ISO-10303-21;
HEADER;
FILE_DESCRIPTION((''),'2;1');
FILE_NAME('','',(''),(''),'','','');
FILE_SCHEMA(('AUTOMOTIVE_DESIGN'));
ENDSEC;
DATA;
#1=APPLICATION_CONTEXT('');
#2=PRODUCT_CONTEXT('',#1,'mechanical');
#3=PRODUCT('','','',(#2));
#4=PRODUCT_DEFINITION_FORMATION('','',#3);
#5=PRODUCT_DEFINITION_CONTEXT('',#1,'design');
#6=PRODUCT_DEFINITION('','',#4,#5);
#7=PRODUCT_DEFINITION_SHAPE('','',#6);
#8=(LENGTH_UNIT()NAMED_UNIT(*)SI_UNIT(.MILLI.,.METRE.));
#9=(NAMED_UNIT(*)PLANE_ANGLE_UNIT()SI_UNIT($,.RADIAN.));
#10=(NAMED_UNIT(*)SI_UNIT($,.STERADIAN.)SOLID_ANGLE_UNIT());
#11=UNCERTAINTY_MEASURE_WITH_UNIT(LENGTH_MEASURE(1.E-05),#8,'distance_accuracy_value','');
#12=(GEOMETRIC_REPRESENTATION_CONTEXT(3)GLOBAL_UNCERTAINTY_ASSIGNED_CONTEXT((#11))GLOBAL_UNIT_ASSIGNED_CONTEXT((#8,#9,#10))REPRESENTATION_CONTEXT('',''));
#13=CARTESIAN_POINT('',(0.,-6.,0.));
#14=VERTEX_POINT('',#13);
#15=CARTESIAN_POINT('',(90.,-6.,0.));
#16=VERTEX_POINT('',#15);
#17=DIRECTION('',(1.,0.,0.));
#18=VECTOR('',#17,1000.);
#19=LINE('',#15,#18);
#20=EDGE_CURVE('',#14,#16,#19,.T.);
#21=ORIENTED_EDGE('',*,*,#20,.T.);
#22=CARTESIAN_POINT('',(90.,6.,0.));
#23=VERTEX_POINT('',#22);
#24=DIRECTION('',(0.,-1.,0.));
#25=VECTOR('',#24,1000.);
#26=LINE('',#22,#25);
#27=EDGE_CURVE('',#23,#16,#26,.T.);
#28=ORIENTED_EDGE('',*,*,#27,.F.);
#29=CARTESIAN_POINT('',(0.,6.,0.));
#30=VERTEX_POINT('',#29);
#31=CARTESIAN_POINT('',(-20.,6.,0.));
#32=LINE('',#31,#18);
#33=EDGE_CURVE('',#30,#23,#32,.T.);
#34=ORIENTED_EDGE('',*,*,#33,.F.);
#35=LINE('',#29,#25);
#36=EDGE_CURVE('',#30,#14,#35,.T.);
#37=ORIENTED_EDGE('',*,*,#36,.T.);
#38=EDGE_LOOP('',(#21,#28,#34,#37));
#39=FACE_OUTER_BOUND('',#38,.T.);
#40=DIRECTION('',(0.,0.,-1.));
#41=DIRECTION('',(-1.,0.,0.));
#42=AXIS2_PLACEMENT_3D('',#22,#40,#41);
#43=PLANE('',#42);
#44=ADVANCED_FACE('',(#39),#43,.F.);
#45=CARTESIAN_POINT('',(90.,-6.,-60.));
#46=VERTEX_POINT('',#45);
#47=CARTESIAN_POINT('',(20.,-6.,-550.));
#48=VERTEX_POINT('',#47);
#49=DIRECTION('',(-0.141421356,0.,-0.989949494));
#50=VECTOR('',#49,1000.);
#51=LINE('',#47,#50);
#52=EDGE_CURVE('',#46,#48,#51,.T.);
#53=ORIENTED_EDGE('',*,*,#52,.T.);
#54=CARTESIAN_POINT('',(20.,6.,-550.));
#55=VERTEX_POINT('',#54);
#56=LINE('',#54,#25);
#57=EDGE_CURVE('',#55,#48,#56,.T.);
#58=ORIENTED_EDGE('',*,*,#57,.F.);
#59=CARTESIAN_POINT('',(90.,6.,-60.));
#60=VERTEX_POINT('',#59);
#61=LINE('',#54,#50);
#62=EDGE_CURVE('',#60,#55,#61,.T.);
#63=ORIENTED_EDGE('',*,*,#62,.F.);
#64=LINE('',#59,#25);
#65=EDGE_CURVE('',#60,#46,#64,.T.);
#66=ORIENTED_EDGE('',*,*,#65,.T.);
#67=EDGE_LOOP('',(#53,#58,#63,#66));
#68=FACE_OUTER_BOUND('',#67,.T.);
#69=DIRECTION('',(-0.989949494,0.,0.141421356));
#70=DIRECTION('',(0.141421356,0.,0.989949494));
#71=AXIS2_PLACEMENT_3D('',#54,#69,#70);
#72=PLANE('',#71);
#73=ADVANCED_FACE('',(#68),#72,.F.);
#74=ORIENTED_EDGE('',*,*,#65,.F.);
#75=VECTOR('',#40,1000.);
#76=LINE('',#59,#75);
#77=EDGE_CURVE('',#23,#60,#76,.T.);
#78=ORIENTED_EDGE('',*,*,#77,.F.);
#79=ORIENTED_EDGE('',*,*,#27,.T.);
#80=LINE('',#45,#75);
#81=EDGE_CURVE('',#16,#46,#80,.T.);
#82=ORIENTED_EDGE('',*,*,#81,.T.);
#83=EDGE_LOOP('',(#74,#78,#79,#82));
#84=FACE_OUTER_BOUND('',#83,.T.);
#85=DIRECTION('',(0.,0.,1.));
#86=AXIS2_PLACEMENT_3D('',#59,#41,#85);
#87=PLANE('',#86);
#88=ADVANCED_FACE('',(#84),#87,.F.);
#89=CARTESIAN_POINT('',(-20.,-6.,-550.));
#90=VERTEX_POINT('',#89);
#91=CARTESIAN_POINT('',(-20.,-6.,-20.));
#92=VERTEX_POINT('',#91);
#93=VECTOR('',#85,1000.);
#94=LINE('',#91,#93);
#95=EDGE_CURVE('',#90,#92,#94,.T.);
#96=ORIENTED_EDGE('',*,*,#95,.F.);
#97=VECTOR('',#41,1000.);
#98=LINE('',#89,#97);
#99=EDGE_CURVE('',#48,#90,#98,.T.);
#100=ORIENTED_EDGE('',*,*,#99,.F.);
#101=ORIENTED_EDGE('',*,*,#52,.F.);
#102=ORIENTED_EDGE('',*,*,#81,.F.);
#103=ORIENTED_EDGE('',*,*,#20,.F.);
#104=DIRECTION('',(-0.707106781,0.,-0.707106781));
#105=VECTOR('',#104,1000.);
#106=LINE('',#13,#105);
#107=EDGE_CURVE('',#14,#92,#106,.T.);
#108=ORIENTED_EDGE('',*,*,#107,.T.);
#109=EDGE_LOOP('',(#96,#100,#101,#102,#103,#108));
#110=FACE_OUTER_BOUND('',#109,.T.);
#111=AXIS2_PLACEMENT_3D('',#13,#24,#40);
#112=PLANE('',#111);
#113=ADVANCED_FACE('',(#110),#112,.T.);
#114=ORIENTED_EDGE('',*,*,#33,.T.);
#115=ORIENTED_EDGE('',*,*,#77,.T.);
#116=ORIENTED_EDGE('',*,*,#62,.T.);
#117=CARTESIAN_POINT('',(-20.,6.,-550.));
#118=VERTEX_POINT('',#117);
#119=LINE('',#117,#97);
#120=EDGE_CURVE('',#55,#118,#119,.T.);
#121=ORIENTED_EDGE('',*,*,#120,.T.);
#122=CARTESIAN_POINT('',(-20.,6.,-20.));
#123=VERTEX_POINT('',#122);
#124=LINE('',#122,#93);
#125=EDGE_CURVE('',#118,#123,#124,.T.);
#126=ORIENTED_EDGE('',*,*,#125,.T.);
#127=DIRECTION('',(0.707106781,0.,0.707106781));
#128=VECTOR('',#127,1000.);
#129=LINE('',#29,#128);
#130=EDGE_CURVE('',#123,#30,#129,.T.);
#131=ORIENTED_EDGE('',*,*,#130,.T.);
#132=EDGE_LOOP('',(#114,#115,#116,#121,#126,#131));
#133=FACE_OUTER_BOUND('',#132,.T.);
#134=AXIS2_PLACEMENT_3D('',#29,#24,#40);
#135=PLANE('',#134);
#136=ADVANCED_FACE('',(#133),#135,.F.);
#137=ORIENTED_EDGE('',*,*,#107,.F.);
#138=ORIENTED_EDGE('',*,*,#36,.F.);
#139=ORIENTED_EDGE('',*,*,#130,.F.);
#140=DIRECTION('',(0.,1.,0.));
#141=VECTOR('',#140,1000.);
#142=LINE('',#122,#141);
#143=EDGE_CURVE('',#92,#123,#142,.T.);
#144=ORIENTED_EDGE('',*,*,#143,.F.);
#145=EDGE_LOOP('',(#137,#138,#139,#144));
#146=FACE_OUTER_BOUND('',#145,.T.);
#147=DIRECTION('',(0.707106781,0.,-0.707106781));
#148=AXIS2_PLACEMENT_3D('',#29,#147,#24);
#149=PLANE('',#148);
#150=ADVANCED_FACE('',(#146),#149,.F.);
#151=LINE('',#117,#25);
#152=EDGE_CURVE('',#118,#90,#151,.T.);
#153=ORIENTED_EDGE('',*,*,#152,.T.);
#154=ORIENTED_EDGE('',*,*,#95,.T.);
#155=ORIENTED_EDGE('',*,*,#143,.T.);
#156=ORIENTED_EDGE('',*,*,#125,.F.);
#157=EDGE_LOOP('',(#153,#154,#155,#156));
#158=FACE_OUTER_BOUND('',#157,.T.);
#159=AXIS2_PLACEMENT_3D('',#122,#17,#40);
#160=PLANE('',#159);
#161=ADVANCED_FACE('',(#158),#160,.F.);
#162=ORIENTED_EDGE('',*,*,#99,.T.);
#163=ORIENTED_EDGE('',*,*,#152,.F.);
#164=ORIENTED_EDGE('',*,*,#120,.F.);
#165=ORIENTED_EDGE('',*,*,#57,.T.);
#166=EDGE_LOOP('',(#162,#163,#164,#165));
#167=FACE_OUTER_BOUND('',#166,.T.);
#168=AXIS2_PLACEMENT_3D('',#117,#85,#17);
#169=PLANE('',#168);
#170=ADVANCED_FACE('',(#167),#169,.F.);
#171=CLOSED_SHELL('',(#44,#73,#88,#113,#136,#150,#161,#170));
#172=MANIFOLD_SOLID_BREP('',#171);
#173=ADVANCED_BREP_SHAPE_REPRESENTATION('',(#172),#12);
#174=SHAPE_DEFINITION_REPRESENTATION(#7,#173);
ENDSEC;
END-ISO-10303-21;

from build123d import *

# Parameters (mm, degrees)
BOSS_EXTRUDE1_DEPTH = 6
CHAMFER1_SIZE       = 20


with BuildPart() as part:
    # Sketch1 → Boss-Extrude1 (new, symmetric)
    with BuildSketch(Plane(origin=(0, 0, 0), x_dir=(1, 0, 0), z_dir=(0, 1, 0))):
        Polygon((-20, 20), (-20, 550), (20, 550), (90, 60), (90, 0), (0, 0), (-20, 0), align=None)
    extrude(amount=BOSS_EXTRUDE1_DEPTH, both=True)

    # Chamfer1
    chamfer1_edges = [part.edges().sort_by_distance(p)[0] for p in [
        (-20, 0, 0),
    ]]
    chamfer(chamfer1_edges, length=CHAMFER1_SIZE)


solid = part.part
